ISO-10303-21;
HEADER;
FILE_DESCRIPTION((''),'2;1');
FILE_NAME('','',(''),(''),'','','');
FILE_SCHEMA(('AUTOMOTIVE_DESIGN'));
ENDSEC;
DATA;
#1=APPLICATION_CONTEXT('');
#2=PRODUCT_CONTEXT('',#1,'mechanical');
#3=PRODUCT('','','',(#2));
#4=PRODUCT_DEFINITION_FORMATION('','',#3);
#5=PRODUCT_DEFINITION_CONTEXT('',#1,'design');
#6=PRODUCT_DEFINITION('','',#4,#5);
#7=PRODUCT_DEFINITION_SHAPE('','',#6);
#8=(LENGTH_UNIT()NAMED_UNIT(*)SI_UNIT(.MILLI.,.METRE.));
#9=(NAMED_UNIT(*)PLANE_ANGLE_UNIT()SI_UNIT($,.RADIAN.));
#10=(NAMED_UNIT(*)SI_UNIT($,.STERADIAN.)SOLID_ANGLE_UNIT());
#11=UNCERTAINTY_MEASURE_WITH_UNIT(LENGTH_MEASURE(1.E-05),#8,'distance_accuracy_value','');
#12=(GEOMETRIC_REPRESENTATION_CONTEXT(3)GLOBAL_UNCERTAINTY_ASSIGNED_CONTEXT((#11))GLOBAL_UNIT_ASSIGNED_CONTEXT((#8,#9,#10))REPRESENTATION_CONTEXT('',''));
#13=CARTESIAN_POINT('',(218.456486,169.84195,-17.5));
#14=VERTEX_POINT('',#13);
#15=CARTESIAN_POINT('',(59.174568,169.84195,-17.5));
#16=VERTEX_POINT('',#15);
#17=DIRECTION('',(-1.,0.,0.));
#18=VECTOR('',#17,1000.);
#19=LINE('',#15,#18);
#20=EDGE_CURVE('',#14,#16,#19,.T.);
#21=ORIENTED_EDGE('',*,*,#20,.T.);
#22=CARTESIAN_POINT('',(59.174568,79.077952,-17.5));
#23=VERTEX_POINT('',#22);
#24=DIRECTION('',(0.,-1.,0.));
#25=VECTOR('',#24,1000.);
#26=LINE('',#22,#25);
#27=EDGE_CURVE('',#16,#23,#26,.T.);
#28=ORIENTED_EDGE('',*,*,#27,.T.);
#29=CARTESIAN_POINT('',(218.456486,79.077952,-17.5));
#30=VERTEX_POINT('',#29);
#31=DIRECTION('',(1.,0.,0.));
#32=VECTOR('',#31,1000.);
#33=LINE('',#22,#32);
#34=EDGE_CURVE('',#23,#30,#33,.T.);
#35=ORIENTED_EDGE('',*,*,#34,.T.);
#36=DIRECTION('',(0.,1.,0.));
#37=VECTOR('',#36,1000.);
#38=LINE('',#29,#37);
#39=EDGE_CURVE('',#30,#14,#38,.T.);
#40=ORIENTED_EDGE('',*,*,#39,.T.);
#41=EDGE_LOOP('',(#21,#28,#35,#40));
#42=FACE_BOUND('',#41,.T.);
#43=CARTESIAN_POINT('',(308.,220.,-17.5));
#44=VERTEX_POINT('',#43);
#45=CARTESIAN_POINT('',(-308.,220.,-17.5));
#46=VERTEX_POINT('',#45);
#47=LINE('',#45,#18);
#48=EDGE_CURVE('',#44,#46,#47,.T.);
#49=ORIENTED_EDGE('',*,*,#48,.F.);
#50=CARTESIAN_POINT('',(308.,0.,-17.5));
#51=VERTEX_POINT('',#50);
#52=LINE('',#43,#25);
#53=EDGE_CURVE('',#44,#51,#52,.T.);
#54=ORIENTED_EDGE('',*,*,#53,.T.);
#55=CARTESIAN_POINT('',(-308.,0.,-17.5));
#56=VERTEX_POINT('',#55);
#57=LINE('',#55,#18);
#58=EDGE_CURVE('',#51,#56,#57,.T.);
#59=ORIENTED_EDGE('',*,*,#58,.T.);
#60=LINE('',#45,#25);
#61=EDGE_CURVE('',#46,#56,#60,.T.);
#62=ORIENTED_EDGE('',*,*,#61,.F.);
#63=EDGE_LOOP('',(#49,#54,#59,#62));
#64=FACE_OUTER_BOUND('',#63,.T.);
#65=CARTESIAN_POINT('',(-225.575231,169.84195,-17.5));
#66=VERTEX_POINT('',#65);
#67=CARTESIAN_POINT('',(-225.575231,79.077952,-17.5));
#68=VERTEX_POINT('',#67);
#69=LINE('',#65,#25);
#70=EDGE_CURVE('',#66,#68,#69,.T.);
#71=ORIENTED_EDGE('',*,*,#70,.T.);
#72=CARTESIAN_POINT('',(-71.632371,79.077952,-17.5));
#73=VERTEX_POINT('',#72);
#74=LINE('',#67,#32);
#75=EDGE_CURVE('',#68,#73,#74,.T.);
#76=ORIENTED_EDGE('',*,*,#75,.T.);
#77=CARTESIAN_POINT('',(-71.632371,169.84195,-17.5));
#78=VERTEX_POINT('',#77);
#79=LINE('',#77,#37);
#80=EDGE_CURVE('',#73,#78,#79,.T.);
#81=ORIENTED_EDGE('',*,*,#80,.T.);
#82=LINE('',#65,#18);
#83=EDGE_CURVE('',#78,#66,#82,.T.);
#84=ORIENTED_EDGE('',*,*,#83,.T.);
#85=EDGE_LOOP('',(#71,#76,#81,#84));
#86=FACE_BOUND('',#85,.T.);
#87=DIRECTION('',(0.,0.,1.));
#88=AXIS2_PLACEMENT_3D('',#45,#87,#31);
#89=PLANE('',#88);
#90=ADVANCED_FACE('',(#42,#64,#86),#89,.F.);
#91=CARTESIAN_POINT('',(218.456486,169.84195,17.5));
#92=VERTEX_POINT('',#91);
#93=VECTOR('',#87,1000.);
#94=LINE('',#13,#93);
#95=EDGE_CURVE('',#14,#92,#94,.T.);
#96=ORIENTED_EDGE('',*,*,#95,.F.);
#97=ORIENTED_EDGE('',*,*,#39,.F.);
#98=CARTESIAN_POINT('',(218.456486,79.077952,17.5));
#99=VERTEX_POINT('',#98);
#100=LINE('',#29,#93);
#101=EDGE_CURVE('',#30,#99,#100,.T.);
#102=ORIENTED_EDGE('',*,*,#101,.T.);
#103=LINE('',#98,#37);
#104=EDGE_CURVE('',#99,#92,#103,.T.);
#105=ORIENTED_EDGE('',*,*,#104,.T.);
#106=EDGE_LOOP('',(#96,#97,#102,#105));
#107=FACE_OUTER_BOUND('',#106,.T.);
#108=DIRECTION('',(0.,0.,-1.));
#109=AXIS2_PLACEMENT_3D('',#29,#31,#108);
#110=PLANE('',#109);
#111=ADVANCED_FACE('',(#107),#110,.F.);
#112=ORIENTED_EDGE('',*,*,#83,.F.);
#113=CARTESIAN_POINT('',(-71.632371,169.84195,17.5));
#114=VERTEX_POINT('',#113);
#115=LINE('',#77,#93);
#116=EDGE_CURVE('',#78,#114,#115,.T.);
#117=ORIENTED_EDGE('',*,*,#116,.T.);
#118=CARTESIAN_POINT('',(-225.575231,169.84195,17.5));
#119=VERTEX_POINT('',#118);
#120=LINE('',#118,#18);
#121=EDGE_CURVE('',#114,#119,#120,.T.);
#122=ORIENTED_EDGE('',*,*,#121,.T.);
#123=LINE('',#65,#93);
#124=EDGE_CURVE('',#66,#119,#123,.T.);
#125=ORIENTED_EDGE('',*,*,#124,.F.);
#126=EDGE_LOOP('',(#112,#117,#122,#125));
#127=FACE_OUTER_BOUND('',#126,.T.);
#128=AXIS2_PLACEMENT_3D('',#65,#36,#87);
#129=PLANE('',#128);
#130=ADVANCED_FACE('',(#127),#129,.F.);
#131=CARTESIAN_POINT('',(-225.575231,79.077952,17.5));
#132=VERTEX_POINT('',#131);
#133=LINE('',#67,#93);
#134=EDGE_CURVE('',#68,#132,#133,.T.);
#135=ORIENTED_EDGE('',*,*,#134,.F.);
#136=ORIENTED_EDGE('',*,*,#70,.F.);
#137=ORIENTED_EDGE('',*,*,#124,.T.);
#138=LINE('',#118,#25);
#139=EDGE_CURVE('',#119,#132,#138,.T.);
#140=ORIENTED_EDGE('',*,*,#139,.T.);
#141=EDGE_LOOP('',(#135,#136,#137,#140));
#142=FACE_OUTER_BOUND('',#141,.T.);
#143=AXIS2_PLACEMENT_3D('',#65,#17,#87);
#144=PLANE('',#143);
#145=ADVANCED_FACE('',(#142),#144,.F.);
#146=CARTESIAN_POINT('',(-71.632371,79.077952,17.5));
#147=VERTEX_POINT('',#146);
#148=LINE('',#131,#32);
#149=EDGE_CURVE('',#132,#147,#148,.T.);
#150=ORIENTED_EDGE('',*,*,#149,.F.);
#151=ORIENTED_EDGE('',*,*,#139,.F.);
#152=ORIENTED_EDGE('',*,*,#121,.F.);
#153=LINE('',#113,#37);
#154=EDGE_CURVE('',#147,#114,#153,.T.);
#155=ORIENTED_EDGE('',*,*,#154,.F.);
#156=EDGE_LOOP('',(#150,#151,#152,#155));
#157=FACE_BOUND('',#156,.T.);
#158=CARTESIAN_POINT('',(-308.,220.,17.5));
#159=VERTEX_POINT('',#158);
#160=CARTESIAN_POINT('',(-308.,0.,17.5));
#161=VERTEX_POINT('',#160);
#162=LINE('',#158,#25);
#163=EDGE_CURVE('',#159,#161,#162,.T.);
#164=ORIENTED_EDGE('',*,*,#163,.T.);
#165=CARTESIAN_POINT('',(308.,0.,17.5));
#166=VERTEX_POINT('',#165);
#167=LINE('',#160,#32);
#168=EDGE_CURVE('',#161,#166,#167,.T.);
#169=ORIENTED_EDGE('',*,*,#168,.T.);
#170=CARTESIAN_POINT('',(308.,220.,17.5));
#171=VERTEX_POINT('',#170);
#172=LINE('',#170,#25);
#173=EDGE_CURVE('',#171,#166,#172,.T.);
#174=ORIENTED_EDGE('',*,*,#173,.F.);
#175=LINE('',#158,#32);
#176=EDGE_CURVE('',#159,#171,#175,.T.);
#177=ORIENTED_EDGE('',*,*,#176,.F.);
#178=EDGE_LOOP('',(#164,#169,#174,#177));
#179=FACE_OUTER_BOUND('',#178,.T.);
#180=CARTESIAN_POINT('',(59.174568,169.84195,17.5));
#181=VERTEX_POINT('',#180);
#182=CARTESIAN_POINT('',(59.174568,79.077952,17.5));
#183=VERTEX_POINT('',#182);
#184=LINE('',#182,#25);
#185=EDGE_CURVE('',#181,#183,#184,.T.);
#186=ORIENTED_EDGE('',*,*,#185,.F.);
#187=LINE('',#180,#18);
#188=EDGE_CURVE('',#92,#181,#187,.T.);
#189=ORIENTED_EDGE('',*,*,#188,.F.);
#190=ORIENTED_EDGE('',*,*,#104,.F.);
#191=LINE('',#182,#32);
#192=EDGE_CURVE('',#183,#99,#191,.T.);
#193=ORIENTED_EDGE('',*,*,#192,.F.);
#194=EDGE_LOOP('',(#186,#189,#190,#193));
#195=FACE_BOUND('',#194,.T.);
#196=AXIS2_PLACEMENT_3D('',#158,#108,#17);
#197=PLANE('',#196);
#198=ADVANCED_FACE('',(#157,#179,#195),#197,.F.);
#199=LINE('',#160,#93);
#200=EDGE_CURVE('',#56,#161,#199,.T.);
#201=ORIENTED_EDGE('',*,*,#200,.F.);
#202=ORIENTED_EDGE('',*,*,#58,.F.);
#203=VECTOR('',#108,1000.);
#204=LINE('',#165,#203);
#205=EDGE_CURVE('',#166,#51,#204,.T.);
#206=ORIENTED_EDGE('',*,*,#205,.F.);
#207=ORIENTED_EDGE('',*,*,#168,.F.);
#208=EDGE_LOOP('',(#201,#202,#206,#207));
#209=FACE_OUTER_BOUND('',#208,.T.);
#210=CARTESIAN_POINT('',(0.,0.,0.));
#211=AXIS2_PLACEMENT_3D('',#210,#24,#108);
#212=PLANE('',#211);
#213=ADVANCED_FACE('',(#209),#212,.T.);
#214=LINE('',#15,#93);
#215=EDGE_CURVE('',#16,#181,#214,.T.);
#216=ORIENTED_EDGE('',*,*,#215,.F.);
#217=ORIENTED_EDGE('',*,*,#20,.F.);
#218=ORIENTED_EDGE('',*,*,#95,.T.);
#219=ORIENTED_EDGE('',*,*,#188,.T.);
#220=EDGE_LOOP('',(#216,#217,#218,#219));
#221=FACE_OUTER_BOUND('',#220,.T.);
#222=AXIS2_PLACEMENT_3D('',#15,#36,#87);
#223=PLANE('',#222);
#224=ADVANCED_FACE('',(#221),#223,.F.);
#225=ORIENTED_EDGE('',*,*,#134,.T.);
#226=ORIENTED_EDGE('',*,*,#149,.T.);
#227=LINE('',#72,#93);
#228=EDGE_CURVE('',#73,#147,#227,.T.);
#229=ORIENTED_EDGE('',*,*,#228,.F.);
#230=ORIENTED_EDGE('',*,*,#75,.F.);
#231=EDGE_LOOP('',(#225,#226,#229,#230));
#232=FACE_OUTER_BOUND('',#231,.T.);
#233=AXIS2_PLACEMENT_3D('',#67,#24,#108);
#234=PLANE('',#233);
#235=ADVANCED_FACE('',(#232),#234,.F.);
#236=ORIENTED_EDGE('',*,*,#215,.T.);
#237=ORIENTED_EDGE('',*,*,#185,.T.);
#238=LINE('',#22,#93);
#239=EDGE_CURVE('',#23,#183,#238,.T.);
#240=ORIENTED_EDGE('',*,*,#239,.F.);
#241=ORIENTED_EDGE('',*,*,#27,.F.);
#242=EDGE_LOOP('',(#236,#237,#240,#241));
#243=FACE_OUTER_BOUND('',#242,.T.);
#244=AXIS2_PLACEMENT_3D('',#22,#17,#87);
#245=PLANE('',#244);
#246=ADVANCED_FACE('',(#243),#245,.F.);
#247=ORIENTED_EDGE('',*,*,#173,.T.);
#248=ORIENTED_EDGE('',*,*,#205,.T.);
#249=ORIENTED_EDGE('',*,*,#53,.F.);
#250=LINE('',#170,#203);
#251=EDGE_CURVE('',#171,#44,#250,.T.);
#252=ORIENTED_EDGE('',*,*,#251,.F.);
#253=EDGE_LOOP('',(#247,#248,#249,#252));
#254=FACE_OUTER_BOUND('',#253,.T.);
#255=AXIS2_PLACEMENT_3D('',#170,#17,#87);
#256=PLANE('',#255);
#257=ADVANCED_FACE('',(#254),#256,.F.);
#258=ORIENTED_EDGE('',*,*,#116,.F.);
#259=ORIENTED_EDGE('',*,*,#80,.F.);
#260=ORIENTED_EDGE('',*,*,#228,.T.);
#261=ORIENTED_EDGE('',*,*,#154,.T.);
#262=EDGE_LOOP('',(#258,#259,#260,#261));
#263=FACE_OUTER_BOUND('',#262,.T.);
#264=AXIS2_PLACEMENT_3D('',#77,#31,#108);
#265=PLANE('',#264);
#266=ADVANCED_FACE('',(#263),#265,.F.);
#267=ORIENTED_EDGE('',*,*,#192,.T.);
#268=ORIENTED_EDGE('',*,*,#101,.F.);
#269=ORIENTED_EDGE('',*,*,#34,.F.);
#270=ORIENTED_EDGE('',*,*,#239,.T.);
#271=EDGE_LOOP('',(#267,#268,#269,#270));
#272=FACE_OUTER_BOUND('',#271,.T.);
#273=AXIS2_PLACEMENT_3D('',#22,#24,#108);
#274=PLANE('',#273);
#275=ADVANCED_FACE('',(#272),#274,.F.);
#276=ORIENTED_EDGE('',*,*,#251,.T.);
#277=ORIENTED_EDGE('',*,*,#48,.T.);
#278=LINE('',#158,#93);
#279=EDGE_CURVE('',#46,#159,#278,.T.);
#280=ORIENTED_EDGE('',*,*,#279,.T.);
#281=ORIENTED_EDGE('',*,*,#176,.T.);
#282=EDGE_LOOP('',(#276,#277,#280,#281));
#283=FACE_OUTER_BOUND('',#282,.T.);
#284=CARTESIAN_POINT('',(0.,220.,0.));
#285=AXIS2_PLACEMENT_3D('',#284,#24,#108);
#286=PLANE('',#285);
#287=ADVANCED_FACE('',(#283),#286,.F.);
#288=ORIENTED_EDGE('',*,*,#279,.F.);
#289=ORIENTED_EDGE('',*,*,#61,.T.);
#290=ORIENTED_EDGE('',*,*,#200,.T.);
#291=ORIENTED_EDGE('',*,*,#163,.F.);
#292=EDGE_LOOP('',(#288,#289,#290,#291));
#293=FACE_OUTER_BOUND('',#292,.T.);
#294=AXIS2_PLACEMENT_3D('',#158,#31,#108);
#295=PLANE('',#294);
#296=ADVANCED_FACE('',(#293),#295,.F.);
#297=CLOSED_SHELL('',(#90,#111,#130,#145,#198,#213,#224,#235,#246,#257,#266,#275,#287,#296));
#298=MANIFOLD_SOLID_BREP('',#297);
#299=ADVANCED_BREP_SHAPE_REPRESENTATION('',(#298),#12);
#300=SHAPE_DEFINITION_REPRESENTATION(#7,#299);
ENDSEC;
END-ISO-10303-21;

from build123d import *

# Parameters (mm, degrees)
SKETCH1_W           = 616
SKETCH1_H           = 35
BOSS_EXTRUDE1_DEPTH = 220
SKETCH2_W           = 153.942859838
SKETCH2_H           = 90.763998287
SKETCH2_W_2         = 159.281918562
CUT_EXTRUDE1_DEPTH  = 381.117087224


with BuildPart() as part:
    # Sketch1 → Boss-Extrude1 (new body)
    with BuildSketch(Plane(origin=(0, 0, 0), x_dir=(1, 0, 0), z_dir=(0, 1, 0))):
        Rectangle(SKETCH1_W, SKETCH1_H)
    extrude(amount=BOSS_EXTRUDE1_DEPTH)

    # Sketch2 → Cut-Extrude1 (cut, through all)
    with BuildSketch(Plane.XY.offset(17.5)):
        with Locations((-148.603801116, 124.459950708)):
            Rectangle(SKETCH2_W, SKETCH2_H)
        with Locations((138.815526791, 124.459950708)):
            Rectangle(SKETCH2_W_2, SKETCH2_H)
    extrude(amount=-CUT_EXTRUDE1_DEPTH, mode=Mode.SUBTRACT)


solid = part.part
